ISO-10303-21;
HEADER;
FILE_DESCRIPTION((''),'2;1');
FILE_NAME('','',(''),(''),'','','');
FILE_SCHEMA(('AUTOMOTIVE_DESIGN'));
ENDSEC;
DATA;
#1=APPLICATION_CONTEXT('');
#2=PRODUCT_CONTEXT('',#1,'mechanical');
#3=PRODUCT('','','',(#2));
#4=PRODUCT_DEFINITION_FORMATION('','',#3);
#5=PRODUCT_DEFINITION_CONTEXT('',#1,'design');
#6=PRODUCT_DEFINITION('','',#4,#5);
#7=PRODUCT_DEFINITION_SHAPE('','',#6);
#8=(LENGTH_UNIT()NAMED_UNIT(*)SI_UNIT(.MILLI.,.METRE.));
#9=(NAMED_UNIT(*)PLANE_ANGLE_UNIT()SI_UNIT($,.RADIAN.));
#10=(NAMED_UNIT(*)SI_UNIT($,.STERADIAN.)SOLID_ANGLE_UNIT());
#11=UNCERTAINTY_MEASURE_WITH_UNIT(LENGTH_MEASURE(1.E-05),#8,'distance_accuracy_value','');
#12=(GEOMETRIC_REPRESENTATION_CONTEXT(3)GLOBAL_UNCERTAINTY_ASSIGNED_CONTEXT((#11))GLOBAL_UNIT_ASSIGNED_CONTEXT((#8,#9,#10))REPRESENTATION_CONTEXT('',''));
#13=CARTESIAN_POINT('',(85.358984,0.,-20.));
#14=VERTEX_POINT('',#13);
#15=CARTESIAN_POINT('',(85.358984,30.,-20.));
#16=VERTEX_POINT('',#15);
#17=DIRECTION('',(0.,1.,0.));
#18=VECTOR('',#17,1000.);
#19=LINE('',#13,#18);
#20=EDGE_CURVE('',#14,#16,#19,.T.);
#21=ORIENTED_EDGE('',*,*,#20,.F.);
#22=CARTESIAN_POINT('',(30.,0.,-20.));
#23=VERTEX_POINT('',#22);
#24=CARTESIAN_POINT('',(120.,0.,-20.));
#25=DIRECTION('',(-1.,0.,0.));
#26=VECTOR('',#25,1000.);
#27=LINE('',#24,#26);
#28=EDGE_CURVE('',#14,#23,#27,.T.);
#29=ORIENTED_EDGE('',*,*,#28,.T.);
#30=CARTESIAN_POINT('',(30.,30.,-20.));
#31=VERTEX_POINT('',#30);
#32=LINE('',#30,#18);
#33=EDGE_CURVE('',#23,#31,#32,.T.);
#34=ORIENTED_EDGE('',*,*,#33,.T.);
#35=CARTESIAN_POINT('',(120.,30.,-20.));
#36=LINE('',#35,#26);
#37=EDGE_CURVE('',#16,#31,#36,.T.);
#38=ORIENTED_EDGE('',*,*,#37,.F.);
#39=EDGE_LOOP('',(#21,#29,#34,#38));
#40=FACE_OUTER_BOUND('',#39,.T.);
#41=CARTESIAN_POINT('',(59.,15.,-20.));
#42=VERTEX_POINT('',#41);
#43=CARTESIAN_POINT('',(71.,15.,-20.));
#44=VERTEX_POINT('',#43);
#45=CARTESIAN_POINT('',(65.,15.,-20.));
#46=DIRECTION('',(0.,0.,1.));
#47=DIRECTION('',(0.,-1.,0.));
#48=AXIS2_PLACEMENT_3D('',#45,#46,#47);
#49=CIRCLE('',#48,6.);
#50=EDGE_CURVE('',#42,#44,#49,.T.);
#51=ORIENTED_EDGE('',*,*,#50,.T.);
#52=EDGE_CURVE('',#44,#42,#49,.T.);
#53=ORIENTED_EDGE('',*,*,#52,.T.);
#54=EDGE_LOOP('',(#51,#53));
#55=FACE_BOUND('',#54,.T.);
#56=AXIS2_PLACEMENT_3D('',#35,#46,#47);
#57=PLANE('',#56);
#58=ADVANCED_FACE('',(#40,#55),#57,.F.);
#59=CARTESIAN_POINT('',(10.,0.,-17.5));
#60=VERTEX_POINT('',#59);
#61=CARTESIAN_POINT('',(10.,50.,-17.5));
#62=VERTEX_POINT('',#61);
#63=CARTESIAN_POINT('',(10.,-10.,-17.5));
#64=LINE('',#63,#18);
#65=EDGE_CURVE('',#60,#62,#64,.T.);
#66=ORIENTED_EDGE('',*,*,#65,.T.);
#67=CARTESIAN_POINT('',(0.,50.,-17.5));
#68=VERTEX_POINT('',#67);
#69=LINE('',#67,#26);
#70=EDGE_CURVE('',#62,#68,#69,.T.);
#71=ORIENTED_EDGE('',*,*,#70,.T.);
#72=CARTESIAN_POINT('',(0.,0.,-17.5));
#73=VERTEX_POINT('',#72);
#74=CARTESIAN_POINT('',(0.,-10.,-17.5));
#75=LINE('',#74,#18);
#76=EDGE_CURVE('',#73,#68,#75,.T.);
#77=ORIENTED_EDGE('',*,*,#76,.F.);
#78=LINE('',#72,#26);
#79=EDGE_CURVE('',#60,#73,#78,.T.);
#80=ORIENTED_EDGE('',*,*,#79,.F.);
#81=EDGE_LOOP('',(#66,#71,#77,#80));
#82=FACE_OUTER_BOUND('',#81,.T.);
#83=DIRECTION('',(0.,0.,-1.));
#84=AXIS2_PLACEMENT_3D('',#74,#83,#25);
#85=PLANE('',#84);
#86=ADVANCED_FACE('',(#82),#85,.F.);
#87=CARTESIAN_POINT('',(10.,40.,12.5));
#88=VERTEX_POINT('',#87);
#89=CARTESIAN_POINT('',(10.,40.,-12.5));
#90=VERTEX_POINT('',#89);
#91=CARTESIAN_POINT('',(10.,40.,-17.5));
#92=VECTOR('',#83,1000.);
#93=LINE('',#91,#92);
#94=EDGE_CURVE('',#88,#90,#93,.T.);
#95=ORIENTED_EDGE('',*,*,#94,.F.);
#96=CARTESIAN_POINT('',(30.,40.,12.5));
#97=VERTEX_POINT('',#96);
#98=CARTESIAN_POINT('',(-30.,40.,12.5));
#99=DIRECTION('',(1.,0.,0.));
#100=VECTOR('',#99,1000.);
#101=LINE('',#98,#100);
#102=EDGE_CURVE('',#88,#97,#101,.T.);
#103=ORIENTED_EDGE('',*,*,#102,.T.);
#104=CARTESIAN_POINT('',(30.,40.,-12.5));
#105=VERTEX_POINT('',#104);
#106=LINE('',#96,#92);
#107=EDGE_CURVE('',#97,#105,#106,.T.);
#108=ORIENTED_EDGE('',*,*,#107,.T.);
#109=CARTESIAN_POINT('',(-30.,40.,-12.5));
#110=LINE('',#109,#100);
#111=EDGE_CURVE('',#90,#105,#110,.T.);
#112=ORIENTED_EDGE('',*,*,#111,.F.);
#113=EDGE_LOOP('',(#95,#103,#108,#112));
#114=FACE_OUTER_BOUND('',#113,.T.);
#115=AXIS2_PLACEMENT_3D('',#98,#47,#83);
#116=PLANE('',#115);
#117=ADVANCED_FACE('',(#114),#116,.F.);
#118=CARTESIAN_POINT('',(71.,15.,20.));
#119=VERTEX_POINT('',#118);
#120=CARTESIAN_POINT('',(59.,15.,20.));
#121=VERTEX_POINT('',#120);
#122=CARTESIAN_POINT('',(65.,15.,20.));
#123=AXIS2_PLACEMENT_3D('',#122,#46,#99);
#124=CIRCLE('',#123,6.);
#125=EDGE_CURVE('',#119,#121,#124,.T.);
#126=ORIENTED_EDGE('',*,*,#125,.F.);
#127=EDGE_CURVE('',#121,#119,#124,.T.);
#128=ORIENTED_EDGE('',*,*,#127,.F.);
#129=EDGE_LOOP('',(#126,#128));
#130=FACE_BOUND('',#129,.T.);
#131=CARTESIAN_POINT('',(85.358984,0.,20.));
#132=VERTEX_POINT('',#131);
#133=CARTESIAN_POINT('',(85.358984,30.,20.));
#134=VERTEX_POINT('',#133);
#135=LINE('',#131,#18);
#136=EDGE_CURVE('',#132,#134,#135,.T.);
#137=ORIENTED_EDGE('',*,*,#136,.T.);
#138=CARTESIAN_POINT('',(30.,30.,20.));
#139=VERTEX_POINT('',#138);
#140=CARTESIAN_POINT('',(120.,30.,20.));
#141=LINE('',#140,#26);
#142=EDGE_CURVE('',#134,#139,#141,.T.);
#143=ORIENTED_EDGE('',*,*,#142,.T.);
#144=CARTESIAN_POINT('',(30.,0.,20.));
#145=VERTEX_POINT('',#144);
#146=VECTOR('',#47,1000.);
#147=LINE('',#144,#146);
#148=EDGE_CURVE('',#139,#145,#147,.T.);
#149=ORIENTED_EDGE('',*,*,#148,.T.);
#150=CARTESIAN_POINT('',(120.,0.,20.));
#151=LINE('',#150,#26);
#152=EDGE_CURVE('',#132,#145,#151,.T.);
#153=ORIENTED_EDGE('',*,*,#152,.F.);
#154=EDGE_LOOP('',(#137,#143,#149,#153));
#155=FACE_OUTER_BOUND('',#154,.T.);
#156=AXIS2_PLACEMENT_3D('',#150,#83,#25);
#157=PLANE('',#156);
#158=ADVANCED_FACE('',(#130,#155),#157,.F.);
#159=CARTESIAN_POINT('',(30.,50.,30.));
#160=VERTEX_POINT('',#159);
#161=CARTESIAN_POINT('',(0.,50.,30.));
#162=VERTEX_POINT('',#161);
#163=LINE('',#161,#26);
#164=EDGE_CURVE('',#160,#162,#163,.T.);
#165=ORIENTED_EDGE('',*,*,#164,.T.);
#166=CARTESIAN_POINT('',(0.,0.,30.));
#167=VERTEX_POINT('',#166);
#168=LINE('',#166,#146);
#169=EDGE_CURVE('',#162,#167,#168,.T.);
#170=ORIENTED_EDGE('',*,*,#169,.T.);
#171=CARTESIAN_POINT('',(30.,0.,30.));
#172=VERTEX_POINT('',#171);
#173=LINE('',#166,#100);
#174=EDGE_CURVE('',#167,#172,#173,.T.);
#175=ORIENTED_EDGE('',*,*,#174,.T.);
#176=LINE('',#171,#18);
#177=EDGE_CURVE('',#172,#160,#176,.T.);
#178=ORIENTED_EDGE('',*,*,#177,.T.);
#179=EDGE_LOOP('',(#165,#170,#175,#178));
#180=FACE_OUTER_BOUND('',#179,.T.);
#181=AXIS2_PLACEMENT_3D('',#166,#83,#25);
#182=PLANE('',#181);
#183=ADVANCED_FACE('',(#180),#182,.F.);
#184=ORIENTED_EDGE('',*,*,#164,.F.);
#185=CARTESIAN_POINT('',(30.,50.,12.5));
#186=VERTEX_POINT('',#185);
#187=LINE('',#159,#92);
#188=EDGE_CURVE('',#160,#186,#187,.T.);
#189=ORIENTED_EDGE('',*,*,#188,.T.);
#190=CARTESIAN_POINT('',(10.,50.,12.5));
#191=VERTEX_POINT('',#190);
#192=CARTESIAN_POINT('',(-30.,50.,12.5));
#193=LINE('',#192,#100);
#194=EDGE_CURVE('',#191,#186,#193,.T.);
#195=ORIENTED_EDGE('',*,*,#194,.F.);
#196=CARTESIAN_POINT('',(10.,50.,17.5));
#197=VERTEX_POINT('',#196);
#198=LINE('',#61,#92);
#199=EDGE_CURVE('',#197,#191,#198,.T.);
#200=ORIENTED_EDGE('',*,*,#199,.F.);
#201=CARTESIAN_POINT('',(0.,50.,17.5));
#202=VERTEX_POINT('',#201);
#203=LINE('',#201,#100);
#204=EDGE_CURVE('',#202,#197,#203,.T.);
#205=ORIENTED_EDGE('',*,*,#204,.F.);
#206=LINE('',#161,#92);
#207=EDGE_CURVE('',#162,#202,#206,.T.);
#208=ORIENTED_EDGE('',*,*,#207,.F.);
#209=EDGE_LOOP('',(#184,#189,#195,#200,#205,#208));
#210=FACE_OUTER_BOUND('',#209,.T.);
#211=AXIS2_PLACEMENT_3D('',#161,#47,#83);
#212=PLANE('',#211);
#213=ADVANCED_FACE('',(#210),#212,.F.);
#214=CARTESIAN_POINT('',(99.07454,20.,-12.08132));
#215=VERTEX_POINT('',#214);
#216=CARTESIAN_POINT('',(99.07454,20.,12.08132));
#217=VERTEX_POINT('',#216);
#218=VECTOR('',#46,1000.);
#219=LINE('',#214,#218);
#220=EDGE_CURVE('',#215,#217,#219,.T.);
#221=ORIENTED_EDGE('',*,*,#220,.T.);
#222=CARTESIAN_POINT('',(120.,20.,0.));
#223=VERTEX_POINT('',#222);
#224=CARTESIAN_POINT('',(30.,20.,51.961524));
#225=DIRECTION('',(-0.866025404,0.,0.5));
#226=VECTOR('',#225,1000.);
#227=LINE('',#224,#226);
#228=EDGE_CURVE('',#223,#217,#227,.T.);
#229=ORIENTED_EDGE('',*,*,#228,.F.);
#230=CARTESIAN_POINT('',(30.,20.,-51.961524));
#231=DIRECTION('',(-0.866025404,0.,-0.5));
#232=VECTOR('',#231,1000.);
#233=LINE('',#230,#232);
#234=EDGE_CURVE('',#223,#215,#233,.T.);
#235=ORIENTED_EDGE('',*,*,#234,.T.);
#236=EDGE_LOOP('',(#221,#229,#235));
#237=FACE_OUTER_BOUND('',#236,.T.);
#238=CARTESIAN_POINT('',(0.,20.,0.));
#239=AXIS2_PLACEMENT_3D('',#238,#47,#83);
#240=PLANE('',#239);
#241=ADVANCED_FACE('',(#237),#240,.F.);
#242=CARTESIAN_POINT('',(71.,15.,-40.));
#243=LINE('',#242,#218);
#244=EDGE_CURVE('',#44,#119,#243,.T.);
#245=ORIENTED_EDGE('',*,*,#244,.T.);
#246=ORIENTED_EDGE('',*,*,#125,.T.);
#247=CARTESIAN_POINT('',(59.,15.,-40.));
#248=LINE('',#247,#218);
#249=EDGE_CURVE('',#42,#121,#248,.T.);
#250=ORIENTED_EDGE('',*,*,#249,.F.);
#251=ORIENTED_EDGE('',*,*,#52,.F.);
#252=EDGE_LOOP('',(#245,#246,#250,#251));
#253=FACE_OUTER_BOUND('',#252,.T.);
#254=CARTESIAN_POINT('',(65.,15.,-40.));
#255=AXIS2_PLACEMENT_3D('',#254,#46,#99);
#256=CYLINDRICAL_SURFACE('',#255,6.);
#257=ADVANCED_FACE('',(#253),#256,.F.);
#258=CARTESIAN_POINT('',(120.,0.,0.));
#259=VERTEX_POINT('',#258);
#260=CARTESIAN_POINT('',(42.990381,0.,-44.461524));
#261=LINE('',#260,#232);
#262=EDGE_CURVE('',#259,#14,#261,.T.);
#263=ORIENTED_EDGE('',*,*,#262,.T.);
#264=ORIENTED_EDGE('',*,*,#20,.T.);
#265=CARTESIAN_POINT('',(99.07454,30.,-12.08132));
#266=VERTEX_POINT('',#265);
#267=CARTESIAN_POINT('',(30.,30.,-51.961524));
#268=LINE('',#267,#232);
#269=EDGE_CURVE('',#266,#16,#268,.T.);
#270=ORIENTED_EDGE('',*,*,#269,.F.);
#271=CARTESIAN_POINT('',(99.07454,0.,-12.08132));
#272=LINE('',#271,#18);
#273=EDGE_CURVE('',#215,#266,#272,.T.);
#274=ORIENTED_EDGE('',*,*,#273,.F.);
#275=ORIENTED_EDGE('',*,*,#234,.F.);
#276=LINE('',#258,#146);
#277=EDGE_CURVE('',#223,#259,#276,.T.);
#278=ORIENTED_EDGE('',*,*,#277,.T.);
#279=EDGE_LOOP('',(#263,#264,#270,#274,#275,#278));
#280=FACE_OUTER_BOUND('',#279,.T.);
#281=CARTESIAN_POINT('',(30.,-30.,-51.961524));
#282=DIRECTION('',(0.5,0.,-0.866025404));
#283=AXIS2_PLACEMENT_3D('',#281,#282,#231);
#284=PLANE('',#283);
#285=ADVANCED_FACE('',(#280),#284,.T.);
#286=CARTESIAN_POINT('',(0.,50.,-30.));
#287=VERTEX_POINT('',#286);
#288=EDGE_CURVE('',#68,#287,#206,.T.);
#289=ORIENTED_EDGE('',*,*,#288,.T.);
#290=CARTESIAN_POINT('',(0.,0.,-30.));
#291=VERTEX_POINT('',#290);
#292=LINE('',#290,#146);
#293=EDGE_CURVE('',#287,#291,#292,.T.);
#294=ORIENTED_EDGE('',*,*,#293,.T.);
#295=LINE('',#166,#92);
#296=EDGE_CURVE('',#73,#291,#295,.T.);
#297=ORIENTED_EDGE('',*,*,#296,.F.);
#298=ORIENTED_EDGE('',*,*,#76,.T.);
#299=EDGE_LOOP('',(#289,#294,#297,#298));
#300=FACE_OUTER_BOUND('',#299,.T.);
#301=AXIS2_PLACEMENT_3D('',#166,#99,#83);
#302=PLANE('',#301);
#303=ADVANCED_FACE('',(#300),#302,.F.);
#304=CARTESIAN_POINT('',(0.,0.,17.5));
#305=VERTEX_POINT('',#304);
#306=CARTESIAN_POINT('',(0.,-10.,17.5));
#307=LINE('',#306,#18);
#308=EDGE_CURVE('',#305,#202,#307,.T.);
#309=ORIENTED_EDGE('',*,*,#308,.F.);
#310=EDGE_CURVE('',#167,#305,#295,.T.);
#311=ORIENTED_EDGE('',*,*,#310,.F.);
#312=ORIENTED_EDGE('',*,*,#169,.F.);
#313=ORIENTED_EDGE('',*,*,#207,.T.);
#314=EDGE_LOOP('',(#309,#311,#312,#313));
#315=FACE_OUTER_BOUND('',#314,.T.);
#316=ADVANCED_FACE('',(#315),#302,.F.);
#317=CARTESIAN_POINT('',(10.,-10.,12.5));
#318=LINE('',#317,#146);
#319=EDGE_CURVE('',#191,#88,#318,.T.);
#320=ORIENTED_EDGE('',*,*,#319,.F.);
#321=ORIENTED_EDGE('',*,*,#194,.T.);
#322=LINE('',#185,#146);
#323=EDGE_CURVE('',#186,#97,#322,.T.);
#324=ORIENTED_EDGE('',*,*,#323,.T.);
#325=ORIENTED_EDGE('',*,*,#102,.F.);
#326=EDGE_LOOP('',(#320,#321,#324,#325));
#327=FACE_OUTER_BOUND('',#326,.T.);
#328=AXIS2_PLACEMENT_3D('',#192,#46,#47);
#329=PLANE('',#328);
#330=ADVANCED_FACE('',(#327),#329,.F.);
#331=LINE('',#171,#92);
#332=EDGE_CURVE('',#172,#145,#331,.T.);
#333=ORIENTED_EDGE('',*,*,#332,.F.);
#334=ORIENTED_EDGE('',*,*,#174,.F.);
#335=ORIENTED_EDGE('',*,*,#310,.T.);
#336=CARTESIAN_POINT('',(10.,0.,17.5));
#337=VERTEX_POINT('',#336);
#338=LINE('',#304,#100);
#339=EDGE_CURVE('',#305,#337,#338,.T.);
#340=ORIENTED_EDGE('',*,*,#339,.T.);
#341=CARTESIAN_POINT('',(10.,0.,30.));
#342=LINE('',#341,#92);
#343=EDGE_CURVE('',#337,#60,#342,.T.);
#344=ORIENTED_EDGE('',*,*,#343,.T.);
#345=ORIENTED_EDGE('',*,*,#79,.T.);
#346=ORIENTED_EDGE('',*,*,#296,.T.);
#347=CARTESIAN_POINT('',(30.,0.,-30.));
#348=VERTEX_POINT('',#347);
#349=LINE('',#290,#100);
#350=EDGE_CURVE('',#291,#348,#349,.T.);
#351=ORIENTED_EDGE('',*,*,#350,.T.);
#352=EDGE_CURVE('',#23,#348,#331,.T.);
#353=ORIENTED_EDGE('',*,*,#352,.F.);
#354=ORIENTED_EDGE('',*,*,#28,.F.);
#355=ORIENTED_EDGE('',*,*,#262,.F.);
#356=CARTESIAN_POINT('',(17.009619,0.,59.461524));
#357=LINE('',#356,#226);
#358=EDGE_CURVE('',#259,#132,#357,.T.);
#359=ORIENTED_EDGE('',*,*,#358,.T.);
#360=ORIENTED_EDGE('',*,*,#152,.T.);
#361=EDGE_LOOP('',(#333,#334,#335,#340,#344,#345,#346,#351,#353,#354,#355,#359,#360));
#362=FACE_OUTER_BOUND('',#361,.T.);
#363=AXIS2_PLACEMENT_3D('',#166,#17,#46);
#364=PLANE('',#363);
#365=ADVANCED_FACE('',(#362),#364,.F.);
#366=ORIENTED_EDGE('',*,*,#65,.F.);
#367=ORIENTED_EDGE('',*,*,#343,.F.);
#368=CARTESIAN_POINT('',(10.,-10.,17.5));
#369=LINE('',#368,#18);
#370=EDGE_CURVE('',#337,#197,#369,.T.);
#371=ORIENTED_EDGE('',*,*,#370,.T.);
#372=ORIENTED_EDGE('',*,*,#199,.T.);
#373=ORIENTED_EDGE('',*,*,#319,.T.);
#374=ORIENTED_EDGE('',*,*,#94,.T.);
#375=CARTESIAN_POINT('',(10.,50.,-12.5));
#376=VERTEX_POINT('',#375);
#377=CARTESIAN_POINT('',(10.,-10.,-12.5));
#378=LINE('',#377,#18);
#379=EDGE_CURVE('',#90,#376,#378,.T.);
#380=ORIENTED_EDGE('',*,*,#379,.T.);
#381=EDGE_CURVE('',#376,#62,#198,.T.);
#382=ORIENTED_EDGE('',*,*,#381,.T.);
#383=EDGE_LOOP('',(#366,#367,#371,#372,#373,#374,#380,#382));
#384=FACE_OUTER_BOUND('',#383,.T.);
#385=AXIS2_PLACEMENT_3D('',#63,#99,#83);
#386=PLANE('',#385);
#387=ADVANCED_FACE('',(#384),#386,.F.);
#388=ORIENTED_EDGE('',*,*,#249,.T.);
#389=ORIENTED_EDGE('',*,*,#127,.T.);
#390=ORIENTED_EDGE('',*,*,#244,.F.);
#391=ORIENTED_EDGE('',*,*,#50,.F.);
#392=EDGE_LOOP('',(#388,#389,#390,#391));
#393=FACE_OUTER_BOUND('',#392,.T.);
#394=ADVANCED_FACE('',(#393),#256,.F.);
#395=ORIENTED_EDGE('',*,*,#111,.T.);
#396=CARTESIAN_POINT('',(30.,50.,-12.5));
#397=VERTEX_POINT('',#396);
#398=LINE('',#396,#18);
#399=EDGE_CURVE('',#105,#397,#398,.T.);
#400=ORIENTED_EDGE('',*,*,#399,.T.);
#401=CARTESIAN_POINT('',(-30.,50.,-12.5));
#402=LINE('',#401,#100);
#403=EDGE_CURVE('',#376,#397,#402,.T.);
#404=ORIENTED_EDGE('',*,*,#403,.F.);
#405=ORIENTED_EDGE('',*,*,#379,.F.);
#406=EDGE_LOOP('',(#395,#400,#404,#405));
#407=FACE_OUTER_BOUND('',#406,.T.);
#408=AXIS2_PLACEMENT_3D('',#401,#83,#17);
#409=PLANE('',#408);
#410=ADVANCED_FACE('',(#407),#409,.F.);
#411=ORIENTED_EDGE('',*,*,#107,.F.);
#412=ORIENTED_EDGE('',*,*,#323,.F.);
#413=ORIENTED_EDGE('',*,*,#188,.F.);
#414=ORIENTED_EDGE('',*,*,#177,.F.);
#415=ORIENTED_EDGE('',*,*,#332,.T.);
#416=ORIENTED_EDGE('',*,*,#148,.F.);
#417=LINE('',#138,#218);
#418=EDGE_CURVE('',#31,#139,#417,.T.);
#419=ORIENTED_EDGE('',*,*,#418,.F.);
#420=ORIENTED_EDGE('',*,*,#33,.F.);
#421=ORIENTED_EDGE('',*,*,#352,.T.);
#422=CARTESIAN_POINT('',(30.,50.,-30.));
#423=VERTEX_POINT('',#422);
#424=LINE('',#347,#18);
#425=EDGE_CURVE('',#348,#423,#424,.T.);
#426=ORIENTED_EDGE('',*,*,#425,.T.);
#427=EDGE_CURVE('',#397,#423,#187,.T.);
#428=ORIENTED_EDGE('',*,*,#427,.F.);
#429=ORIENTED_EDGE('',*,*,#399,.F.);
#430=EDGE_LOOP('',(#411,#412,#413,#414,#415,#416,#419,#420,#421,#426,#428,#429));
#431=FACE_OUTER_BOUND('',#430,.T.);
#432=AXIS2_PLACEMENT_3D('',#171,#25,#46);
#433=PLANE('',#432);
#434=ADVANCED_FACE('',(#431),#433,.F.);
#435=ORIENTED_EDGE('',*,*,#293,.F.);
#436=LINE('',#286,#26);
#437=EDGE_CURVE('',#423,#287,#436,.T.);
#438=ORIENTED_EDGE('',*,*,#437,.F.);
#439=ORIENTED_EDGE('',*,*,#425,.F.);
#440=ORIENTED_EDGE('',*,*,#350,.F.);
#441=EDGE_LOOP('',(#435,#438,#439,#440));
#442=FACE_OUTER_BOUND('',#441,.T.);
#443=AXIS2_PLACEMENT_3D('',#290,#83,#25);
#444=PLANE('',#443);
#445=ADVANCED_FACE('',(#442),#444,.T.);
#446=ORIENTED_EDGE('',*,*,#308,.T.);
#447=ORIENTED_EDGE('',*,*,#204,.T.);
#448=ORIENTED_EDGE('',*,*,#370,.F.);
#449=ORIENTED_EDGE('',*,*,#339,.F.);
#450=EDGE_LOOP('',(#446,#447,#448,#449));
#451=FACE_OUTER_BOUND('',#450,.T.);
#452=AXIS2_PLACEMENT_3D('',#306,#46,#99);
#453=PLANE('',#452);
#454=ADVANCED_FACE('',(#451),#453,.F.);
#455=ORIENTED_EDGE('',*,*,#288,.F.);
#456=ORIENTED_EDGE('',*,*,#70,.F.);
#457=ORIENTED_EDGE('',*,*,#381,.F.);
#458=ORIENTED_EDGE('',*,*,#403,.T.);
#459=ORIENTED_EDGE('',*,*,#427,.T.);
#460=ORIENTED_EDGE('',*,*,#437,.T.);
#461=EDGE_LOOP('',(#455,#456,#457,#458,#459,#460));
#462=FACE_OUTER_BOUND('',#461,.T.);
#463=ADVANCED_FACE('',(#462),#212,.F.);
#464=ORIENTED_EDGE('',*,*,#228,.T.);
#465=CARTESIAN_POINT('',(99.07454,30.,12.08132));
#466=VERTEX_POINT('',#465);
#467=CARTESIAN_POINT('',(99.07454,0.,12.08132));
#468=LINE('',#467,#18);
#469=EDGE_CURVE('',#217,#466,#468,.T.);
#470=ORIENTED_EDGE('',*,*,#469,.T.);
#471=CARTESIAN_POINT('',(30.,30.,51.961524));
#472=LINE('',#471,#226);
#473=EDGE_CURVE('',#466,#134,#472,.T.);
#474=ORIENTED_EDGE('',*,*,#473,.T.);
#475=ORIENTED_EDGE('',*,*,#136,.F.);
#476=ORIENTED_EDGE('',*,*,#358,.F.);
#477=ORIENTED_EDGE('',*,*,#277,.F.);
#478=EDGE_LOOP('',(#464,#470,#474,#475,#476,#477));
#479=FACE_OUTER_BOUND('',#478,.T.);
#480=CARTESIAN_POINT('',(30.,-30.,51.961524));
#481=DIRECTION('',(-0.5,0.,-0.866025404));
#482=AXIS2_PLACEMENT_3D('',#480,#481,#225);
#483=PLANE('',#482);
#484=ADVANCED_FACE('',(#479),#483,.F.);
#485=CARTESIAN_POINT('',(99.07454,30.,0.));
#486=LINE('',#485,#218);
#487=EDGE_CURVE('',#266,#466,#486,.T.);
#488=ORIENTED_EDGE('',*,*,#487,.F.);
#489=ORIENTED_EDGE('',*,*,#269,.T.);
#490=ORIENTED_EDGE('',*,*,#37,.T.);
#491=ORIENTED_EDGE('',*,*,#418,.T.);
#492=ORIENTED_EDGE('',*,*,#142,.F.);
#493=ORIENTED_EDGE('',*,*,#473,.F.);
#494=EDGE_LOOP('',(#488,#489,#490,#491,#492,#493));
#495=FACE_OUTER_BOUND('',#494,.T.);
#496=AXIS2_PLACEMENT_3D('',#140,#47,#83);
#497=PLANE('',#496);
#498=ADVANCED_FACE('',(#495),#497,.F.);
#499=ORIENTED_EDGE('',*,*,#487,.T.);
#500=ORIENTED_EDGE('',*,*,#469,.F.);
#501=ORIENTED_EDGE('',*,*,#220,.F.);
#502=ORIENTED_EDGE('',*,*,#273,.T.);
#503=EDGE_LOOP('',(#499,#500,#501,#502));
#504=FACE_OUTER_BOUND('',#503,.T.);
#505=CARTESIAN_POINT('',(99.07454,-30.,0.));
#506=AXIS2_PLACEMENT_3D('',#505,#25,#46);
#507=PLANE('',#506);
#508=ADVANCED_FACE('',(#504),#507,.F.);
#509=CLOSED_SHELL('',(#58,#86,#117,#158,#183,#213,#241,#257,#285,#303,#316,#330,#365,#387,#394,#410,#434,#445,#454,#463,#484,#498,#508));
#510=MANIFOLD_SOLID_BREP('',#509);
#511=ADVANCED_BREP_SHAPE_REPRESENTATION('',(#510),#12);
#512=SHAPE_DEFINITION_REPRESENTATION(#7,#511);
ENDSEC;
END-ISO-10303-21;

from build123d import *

# Parameters (mm, degrees)
BASE_BLOCK_SKETCH_W        = 30
BASE_BLOCK_SKETCH_H        = 50
BASE_BLOCK_DEPTH           = 30
THROUGH_SLOT_SKETCH_W      = 10
THROUGH_SLOT_SKETCH_H      = 35
THROUGH_SLOT_DEPTH         = 60
STEP_NOTCH_SKETCH_W        = 25
STEP_NOTCH_SKETCH_H        = 10
STEP_NOTCH_DEPTH           = 60
NOSE_BOSS_SKETCH_W         = 40
NOSE_BOSS_SKETCH_H         = 30
NOSE_BOSS_DEPTH            = 90
CORNER_CUT_SKETCH_R        = 6
CORNER_CUT_DEPTH           = 60
NOSE_TAPER_30DEG_CUT_DEPTH = 60
SIDE_POCKET_SKETCH_W       = 22.012832553
SIDE_POCKET_SKETCH_H       = 24.1626403
SIDE_POCKET_10MM_DEPTH     = 10
NOSE_PROFILE_CUT_DEPTH     = 30


with BuildPart() as part:
    # Base Block Sketch → Base Block (new, symmetric)
    with BuildSketch(Plane.XY):
        with Locations((15, 25)):
            Rectangle(BASE_BLOCK_SKETCH_W, BASE_BLOCK_SKETCH_H)
    extrude(amount=BASE_BLOCK_DEPTH, both=True)

    # Through Slot Sketch → Through Slot (cut)
    with BuildSketch(Plane(origin=(0, 50, 0), x_dir=(1, 0, 0), z_dir=(0, 1, 0))):
        with Locations((5, 0)):
            Rectangle(THROUGH_SLOT_SKETCH_W, THROUGH_SLOT_SKETCH_H)
    extrude(amount=-THROUGH_SLOT_DEPTH, mode=Mode.SUBTRACT)

    # Step Notch Sketch → Step Notch (cut)
    with BuildSketch(Plane(origin=(30, 0, 0), x_dir=(0, 0, -1), z_dir=(1, 0, 0))):
        with Locations((0, 45)):
            Rectangle(STEP_NOTCH_SKETCH_W, STEP_NOTCH_SKETCH_H)
    extrude(amount=-STEP_NOTCH_DEPTH, mode=Mode.SUBTRACT)

    # Nose Boss Sketch → Nose Boss (add)
    with BuildSketch(Plane(origin=(30, 0, 0), x_dir=(0, 0, -1), z_dir=(1, 0, 0))):
        with Locations((0, 15)):
            Rectangle(NOSE_BOSS_SKETCH_W, NOSE_BOSS_SKETCH_H)
    extrude(amount=NOSE_BOSS_DEPTH)

    # Corner Cut Sketch → Corner Cut (cut)
    with BuildSketch(Plane.XY.offset(20)):
        with Locations((65, 15)):
            Circle(CORNER_CUT_SKETCH_R)
    extrude(amount=-CORNER_CUT_DEPTH, mode=Mode.SUBTRACT)

    # Nose Taper 30deg Sketch → Nose Taper 30deg Cut (cut)
    with BuildSketch(Plane(origin=(0, 30, 0), x_dir=(1, 0, 0), z_dir=(0, 1, 0))):
        Polygon((99.074539678, -20), (120, -20), (120, 0), (99.074539678, -12.08132015), align=None)
        Polygon((99.074539678, 12.08132015), (120, 0), (120, 20), (99.074539678, 20), align=None)
    extrude(amount=-NOSE_TAPER_30DEG_CUT_DEPTH, mode=Mode.SUBTRACT)

    # Side Pocket Sketch → Side Pocket 10mm (cut)
    with BuildSketch(Plane(origin=(0, 30, 0), x_dir=(1, 0, 0), z_dir=(0, 1, 0))):
        with Locations((110.080955955, 0)):
            Rectangle(SIDE_POCKET_SKETCH_W, SIDE_POCKET_SKETCH_H)
    extrude(amount=-SIDE_POCKET_10MM_DEPTH, mode=Mode.SUBTRACT)

    # Nose Profile Sketch → Nose Profile Cut (cut)
    with BuildSketch(Plane(origin=(0, 30, 0), x_dir=(1, 0, 0), z_dir=(0, 1, 0))):
        Polygon((85.358983849, 20), (99.074539678, 12.08132015), (99.074539678, 20), align=None)
        Polygon((99.074539678, -20), (99.074539678, -12.08132015), (85.358983849, -20), align=None)
    extrude(amount=-NOSE_PROFILE_CUT_DEPTH, mode=Mode.SUBTRACT)


solid = part.part
